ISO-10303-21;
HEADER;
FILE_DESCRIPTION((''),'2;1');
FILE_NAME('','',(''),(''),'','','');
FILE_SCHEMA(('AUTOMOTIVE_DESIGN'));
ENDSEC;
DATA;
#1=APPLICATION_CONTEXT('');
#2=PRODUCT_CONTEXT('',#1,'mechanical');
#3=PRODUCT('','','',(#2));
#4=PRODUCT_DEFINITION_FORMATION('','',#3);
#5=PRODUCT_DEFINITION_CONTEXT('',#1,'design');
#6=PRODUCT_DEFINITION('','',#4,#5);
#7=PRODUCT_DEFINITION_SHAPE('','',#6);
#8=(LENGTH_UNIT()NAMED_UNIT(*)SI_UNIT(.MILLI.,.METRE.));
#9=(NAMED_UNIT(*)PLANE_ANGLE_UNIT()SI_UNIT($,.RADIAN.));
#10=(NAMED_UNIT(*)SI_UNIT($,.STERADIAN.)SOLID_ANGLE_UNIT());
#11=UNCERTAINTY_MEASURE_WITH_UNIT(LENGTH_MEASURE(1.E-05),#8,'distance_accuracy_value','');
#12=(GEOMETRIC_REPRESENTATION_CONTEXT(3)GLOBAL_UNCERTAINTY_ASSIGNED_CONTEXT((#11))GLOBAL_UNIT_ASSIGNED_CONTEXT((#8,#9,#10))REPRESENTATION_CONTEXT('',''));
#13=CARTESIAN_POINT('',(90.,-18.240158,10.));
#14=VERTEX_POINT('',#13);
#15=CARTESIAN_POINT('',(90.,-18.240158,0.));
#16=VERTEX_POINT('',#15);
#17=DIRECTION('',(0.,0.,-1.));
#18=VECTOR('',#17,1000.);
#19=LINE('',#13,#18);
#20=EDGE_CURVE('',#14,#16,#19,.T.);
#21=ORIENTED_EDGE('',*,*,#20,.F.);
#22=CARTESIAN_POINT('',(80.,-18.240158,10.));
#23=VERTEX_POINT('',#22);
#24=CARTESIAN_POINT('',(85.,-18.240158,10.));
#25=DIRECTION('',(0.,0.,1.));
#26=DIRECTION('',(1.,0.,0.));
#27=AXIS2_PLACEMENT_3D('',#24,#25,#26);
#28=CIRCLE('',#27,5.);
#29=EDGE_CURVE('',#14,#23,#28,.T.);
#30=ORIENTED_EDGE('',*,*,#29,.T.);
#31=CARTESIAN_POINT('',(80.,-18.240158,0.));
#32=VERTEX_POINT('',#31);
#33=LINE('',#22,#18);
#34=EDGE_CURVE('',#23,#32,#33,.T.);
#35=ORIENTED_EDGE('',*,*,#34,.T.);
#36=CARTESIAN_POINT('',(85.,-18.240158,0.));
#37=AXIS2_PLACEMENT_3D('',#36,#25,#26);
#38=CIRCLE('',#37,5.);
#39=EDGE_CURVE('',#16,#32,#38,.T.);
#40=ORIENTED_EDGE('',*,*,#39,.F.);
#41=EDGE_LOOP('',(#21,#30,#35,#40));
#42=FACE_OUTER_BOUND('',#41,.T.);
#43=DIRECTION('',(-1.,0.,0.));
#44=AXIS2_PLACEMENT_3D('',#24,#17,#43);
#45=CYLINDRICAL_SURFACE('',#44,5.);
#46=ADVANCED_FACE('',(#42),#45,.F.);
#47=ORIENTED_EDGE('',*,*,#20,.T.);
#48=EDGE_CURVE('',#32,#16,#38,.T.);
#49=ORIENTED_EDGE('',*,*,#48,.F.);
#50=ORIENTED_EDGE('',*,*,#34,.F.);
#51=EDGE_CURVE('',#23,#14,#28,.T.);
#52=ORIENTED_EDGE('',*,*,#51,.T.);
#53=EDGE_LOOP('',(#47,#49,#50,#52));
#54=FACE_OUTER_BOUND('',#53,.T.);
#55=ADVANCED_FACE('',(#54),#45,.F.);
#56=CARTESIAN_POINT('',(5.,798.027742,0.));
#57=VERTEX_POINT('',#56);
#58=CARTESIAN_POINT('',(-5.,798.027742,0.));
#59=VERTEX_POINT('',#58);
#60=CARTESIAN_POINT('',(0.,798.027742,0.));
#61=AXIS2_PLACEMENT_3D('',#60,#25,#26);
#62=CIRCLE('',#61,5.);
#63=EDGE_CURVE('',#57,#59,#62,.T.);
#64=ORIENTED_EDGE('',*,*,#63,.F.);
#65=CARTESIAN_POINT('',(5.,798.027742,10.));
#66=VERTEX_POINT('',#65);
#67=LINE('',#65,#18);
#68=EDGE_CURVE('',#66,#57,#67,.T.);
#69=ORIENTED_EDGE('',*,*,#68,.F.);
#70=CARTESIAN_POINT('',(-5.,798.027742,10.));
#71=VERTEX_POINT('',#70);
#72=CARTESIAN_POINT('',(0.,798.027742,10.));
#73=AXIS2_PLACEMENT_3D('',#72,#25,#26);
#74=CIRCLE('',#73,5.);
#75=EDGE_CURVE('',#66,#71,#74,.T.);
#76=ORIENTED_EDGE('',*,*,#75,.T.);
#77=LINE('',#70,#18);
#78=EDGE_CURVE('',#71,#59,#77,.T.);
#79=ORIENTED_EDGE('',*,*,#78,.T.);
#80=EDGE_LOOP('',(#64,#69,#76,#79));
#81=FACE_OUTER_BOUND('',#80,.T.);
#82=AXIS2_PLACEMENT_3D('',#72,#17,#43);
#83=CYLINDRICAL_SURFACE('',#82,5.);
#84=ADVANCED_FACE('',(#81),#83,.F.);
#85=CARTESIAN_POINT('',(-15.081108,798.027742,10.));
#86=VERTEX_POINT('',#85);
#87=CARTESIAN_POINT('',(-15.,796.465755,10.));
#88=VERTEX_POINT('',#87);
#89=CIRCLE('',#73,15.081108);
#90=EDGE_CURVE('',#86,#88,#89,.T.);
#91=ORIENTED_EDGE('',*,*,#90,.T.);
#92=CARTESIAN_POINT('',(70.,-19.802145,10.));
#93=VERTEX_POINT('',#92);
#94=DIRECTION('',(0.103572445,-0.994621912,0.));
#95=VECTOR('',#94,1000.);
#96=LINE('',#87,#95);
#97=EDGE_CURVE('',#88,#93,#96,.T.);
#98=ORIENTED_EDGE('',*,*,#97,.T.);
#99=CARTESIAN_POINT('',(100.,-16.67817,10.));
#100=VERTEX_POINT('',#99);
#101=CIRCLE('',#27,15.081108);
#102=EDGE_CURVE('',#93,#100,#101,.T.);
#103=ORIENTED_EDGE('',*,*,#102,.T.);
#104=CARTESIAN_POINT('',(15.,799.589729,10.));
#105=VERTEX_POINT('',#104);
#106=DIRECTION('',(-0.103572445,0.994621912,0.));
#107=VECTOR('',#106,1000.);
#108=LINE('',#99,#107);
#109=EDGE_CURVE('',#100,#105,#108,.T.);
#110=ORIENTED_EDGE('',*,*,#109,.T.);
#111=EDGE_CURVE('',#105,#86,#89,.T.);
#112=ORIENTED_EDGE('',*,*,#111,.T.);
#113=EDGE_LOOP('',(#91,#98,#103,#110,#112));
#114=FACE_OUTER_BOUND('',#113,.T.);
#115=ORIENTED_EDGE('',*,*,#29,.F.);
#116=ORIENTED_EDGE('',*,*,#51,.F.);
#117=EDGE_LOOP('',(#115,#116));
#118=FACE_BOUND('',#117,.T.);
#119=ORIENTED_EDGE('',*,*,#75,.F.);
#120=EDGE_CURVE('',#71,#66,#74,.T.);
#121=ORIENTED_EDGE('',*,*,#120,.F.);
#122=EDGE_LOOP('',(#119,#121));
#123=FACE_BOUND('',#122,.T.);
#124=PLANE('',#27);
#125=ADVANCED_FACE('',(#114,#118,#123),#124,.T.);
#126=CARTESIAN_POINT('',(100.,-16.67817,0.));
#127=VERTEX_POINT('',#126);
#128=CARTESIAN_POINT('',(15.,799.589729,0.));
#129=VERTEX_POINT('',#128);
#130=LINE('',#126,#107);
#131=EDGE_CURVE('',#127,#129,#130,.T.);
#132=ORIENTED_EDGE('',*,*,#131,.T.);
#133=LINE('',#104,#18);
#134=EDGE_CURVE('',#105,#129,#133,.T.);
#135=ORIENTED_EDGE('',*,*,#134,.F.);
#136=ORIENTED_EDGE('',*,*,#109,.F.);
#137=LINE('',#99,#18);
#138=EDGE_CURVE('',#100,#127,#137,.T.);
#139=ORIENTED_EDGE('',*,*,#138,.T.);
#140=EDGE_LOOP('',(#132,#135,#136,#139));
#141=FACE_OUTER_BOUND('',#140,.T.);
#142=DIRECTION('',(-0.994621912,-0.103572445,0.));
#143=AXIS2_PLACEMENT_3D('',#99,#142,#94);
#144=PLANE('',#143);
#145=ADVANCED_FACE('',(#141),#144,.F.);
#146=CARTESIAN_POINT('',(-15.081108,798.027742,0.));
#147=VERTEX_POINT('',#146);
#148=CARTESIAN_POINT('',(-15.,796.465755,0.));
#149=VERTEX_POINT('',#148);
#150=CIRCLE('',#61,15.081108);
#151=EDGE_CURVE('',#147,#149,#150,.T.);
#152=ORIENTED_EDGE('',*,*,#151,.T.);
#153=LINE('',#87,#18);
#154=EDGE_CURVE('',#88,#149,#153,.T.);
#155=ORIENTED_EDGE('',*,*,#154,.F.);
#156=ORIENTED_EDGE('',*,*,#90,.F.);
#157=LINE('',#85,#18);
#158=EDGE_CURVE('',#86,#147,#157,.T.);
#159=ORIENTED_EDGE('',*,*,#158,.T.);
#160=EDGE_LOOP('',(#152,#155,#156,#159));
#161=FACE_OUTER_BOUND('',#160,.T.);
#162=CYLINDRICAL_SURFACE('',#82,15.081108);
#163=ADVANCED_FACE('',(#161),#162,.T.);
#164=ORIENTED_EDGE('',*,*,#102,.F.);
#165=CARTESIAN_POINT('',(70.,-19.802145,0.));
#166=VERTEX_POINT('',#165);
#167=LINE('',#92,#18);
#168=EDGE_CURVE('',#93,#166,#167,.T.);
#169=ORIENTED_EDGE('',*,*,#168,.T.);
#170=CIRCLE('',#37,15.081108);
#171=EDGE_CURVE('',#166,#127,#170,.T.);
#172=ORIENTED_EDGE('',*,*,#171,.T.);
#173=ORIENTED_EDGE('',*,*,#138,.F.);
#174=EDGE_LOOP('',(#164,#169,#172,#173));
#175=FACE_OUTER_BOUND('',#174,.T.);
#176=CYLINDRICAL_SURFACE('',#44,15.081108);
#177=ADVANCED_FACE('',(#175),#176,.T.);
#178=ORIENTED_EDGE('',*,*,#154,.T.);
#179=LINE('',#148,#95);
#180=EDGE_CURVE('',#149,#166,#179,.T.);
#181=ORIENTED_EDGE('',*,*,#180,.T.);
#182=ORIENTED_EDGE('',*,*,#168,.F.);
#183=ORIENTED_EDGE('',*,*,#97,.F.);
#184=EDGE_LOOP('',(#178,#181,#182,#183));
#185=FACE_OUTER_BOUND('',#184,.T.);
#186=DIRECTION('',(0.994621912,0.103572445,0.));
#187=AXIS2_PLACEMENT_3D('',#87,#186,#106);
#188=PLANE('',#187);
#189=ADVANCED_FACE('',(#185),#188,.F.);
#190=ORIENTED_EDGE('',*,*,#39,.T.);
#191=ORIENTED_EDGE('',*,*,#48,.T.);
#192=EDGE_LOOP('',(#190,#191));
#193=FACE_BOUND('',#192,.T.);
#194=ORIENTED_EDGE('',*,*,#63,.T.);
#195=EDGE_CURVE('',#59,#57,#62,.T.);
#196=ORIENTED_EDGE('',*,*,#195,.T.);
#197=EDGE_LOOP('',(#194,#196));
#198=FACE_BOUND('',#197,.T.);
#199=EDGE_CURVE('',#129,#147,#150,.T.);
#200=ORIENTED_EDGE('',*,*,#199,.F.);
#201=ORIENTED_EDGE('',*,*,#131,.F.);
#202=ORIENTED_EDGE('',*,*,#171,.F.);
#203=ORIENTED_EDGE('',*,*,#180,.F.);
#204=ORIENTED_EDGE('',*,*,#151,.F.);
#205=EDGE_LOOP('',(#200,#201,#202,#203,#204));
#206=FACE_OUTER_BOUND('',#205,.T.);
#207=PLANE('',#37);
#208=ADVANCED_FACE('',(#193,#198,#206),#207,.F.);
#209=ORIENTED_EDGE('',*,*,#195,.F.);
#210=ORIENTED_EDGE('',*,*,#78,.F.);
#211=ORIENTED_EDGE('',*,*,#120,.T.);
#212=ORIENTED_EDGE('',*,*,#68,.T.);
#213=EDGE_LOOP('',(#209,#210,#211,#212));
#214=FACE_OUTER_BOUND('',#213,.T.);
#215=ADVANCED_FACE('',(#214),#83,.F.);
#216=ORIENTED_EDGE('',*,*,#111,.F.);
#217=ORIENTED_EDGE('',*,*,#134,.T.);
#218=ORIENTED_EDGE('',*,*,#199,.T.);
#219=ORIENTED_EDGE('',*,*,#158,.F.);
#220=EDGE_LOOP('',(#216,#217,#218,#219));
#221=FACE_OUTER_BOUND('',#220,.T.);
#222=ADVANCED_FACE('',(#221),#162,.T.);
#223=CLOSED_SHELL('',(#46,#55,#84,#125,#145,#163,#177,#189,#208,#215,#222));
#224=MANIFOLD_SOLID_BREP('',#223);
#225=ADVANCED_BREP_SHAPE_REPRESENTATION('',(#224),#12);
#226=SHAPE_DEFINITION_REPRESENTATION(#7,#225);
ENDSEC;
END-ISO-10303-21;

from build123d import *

# Parameters (mm, degrees)
SKETCH3_R           = 5
BOSS_EXTRUDE1_DEPTH = 10


with BuildPart() as part:
    # Sketch3 → Boss-Extrude1 (new body)
    with BuildSketch(Plane.XY):
        with BuildLine():
            Line((-15, 796.465754902), (70, -19.802144846))
            ThreePointArc((70, -19.802144846), (86.561987186, -33.24015766), (100, -16.678170473))
            Line((100, -16.678170473), (15, 799.589729274))
            ThreePointArc((15, 799.589729274), (-1.561987186, 813.027742088), (-15, 796.465754902))
        make_face()
        with Locations((0, 798.027742088)):
            Circle(SKETCH3_R, mode=Mode.SUBTRACT)
        with Locations((85, -18.24015766)):
            Circle(SKETCH3_R, mode=Mode.SUBTRACT)
    extrude(amount=BOSS_EXTRUDE1_DEPTH)


solid = part.part
